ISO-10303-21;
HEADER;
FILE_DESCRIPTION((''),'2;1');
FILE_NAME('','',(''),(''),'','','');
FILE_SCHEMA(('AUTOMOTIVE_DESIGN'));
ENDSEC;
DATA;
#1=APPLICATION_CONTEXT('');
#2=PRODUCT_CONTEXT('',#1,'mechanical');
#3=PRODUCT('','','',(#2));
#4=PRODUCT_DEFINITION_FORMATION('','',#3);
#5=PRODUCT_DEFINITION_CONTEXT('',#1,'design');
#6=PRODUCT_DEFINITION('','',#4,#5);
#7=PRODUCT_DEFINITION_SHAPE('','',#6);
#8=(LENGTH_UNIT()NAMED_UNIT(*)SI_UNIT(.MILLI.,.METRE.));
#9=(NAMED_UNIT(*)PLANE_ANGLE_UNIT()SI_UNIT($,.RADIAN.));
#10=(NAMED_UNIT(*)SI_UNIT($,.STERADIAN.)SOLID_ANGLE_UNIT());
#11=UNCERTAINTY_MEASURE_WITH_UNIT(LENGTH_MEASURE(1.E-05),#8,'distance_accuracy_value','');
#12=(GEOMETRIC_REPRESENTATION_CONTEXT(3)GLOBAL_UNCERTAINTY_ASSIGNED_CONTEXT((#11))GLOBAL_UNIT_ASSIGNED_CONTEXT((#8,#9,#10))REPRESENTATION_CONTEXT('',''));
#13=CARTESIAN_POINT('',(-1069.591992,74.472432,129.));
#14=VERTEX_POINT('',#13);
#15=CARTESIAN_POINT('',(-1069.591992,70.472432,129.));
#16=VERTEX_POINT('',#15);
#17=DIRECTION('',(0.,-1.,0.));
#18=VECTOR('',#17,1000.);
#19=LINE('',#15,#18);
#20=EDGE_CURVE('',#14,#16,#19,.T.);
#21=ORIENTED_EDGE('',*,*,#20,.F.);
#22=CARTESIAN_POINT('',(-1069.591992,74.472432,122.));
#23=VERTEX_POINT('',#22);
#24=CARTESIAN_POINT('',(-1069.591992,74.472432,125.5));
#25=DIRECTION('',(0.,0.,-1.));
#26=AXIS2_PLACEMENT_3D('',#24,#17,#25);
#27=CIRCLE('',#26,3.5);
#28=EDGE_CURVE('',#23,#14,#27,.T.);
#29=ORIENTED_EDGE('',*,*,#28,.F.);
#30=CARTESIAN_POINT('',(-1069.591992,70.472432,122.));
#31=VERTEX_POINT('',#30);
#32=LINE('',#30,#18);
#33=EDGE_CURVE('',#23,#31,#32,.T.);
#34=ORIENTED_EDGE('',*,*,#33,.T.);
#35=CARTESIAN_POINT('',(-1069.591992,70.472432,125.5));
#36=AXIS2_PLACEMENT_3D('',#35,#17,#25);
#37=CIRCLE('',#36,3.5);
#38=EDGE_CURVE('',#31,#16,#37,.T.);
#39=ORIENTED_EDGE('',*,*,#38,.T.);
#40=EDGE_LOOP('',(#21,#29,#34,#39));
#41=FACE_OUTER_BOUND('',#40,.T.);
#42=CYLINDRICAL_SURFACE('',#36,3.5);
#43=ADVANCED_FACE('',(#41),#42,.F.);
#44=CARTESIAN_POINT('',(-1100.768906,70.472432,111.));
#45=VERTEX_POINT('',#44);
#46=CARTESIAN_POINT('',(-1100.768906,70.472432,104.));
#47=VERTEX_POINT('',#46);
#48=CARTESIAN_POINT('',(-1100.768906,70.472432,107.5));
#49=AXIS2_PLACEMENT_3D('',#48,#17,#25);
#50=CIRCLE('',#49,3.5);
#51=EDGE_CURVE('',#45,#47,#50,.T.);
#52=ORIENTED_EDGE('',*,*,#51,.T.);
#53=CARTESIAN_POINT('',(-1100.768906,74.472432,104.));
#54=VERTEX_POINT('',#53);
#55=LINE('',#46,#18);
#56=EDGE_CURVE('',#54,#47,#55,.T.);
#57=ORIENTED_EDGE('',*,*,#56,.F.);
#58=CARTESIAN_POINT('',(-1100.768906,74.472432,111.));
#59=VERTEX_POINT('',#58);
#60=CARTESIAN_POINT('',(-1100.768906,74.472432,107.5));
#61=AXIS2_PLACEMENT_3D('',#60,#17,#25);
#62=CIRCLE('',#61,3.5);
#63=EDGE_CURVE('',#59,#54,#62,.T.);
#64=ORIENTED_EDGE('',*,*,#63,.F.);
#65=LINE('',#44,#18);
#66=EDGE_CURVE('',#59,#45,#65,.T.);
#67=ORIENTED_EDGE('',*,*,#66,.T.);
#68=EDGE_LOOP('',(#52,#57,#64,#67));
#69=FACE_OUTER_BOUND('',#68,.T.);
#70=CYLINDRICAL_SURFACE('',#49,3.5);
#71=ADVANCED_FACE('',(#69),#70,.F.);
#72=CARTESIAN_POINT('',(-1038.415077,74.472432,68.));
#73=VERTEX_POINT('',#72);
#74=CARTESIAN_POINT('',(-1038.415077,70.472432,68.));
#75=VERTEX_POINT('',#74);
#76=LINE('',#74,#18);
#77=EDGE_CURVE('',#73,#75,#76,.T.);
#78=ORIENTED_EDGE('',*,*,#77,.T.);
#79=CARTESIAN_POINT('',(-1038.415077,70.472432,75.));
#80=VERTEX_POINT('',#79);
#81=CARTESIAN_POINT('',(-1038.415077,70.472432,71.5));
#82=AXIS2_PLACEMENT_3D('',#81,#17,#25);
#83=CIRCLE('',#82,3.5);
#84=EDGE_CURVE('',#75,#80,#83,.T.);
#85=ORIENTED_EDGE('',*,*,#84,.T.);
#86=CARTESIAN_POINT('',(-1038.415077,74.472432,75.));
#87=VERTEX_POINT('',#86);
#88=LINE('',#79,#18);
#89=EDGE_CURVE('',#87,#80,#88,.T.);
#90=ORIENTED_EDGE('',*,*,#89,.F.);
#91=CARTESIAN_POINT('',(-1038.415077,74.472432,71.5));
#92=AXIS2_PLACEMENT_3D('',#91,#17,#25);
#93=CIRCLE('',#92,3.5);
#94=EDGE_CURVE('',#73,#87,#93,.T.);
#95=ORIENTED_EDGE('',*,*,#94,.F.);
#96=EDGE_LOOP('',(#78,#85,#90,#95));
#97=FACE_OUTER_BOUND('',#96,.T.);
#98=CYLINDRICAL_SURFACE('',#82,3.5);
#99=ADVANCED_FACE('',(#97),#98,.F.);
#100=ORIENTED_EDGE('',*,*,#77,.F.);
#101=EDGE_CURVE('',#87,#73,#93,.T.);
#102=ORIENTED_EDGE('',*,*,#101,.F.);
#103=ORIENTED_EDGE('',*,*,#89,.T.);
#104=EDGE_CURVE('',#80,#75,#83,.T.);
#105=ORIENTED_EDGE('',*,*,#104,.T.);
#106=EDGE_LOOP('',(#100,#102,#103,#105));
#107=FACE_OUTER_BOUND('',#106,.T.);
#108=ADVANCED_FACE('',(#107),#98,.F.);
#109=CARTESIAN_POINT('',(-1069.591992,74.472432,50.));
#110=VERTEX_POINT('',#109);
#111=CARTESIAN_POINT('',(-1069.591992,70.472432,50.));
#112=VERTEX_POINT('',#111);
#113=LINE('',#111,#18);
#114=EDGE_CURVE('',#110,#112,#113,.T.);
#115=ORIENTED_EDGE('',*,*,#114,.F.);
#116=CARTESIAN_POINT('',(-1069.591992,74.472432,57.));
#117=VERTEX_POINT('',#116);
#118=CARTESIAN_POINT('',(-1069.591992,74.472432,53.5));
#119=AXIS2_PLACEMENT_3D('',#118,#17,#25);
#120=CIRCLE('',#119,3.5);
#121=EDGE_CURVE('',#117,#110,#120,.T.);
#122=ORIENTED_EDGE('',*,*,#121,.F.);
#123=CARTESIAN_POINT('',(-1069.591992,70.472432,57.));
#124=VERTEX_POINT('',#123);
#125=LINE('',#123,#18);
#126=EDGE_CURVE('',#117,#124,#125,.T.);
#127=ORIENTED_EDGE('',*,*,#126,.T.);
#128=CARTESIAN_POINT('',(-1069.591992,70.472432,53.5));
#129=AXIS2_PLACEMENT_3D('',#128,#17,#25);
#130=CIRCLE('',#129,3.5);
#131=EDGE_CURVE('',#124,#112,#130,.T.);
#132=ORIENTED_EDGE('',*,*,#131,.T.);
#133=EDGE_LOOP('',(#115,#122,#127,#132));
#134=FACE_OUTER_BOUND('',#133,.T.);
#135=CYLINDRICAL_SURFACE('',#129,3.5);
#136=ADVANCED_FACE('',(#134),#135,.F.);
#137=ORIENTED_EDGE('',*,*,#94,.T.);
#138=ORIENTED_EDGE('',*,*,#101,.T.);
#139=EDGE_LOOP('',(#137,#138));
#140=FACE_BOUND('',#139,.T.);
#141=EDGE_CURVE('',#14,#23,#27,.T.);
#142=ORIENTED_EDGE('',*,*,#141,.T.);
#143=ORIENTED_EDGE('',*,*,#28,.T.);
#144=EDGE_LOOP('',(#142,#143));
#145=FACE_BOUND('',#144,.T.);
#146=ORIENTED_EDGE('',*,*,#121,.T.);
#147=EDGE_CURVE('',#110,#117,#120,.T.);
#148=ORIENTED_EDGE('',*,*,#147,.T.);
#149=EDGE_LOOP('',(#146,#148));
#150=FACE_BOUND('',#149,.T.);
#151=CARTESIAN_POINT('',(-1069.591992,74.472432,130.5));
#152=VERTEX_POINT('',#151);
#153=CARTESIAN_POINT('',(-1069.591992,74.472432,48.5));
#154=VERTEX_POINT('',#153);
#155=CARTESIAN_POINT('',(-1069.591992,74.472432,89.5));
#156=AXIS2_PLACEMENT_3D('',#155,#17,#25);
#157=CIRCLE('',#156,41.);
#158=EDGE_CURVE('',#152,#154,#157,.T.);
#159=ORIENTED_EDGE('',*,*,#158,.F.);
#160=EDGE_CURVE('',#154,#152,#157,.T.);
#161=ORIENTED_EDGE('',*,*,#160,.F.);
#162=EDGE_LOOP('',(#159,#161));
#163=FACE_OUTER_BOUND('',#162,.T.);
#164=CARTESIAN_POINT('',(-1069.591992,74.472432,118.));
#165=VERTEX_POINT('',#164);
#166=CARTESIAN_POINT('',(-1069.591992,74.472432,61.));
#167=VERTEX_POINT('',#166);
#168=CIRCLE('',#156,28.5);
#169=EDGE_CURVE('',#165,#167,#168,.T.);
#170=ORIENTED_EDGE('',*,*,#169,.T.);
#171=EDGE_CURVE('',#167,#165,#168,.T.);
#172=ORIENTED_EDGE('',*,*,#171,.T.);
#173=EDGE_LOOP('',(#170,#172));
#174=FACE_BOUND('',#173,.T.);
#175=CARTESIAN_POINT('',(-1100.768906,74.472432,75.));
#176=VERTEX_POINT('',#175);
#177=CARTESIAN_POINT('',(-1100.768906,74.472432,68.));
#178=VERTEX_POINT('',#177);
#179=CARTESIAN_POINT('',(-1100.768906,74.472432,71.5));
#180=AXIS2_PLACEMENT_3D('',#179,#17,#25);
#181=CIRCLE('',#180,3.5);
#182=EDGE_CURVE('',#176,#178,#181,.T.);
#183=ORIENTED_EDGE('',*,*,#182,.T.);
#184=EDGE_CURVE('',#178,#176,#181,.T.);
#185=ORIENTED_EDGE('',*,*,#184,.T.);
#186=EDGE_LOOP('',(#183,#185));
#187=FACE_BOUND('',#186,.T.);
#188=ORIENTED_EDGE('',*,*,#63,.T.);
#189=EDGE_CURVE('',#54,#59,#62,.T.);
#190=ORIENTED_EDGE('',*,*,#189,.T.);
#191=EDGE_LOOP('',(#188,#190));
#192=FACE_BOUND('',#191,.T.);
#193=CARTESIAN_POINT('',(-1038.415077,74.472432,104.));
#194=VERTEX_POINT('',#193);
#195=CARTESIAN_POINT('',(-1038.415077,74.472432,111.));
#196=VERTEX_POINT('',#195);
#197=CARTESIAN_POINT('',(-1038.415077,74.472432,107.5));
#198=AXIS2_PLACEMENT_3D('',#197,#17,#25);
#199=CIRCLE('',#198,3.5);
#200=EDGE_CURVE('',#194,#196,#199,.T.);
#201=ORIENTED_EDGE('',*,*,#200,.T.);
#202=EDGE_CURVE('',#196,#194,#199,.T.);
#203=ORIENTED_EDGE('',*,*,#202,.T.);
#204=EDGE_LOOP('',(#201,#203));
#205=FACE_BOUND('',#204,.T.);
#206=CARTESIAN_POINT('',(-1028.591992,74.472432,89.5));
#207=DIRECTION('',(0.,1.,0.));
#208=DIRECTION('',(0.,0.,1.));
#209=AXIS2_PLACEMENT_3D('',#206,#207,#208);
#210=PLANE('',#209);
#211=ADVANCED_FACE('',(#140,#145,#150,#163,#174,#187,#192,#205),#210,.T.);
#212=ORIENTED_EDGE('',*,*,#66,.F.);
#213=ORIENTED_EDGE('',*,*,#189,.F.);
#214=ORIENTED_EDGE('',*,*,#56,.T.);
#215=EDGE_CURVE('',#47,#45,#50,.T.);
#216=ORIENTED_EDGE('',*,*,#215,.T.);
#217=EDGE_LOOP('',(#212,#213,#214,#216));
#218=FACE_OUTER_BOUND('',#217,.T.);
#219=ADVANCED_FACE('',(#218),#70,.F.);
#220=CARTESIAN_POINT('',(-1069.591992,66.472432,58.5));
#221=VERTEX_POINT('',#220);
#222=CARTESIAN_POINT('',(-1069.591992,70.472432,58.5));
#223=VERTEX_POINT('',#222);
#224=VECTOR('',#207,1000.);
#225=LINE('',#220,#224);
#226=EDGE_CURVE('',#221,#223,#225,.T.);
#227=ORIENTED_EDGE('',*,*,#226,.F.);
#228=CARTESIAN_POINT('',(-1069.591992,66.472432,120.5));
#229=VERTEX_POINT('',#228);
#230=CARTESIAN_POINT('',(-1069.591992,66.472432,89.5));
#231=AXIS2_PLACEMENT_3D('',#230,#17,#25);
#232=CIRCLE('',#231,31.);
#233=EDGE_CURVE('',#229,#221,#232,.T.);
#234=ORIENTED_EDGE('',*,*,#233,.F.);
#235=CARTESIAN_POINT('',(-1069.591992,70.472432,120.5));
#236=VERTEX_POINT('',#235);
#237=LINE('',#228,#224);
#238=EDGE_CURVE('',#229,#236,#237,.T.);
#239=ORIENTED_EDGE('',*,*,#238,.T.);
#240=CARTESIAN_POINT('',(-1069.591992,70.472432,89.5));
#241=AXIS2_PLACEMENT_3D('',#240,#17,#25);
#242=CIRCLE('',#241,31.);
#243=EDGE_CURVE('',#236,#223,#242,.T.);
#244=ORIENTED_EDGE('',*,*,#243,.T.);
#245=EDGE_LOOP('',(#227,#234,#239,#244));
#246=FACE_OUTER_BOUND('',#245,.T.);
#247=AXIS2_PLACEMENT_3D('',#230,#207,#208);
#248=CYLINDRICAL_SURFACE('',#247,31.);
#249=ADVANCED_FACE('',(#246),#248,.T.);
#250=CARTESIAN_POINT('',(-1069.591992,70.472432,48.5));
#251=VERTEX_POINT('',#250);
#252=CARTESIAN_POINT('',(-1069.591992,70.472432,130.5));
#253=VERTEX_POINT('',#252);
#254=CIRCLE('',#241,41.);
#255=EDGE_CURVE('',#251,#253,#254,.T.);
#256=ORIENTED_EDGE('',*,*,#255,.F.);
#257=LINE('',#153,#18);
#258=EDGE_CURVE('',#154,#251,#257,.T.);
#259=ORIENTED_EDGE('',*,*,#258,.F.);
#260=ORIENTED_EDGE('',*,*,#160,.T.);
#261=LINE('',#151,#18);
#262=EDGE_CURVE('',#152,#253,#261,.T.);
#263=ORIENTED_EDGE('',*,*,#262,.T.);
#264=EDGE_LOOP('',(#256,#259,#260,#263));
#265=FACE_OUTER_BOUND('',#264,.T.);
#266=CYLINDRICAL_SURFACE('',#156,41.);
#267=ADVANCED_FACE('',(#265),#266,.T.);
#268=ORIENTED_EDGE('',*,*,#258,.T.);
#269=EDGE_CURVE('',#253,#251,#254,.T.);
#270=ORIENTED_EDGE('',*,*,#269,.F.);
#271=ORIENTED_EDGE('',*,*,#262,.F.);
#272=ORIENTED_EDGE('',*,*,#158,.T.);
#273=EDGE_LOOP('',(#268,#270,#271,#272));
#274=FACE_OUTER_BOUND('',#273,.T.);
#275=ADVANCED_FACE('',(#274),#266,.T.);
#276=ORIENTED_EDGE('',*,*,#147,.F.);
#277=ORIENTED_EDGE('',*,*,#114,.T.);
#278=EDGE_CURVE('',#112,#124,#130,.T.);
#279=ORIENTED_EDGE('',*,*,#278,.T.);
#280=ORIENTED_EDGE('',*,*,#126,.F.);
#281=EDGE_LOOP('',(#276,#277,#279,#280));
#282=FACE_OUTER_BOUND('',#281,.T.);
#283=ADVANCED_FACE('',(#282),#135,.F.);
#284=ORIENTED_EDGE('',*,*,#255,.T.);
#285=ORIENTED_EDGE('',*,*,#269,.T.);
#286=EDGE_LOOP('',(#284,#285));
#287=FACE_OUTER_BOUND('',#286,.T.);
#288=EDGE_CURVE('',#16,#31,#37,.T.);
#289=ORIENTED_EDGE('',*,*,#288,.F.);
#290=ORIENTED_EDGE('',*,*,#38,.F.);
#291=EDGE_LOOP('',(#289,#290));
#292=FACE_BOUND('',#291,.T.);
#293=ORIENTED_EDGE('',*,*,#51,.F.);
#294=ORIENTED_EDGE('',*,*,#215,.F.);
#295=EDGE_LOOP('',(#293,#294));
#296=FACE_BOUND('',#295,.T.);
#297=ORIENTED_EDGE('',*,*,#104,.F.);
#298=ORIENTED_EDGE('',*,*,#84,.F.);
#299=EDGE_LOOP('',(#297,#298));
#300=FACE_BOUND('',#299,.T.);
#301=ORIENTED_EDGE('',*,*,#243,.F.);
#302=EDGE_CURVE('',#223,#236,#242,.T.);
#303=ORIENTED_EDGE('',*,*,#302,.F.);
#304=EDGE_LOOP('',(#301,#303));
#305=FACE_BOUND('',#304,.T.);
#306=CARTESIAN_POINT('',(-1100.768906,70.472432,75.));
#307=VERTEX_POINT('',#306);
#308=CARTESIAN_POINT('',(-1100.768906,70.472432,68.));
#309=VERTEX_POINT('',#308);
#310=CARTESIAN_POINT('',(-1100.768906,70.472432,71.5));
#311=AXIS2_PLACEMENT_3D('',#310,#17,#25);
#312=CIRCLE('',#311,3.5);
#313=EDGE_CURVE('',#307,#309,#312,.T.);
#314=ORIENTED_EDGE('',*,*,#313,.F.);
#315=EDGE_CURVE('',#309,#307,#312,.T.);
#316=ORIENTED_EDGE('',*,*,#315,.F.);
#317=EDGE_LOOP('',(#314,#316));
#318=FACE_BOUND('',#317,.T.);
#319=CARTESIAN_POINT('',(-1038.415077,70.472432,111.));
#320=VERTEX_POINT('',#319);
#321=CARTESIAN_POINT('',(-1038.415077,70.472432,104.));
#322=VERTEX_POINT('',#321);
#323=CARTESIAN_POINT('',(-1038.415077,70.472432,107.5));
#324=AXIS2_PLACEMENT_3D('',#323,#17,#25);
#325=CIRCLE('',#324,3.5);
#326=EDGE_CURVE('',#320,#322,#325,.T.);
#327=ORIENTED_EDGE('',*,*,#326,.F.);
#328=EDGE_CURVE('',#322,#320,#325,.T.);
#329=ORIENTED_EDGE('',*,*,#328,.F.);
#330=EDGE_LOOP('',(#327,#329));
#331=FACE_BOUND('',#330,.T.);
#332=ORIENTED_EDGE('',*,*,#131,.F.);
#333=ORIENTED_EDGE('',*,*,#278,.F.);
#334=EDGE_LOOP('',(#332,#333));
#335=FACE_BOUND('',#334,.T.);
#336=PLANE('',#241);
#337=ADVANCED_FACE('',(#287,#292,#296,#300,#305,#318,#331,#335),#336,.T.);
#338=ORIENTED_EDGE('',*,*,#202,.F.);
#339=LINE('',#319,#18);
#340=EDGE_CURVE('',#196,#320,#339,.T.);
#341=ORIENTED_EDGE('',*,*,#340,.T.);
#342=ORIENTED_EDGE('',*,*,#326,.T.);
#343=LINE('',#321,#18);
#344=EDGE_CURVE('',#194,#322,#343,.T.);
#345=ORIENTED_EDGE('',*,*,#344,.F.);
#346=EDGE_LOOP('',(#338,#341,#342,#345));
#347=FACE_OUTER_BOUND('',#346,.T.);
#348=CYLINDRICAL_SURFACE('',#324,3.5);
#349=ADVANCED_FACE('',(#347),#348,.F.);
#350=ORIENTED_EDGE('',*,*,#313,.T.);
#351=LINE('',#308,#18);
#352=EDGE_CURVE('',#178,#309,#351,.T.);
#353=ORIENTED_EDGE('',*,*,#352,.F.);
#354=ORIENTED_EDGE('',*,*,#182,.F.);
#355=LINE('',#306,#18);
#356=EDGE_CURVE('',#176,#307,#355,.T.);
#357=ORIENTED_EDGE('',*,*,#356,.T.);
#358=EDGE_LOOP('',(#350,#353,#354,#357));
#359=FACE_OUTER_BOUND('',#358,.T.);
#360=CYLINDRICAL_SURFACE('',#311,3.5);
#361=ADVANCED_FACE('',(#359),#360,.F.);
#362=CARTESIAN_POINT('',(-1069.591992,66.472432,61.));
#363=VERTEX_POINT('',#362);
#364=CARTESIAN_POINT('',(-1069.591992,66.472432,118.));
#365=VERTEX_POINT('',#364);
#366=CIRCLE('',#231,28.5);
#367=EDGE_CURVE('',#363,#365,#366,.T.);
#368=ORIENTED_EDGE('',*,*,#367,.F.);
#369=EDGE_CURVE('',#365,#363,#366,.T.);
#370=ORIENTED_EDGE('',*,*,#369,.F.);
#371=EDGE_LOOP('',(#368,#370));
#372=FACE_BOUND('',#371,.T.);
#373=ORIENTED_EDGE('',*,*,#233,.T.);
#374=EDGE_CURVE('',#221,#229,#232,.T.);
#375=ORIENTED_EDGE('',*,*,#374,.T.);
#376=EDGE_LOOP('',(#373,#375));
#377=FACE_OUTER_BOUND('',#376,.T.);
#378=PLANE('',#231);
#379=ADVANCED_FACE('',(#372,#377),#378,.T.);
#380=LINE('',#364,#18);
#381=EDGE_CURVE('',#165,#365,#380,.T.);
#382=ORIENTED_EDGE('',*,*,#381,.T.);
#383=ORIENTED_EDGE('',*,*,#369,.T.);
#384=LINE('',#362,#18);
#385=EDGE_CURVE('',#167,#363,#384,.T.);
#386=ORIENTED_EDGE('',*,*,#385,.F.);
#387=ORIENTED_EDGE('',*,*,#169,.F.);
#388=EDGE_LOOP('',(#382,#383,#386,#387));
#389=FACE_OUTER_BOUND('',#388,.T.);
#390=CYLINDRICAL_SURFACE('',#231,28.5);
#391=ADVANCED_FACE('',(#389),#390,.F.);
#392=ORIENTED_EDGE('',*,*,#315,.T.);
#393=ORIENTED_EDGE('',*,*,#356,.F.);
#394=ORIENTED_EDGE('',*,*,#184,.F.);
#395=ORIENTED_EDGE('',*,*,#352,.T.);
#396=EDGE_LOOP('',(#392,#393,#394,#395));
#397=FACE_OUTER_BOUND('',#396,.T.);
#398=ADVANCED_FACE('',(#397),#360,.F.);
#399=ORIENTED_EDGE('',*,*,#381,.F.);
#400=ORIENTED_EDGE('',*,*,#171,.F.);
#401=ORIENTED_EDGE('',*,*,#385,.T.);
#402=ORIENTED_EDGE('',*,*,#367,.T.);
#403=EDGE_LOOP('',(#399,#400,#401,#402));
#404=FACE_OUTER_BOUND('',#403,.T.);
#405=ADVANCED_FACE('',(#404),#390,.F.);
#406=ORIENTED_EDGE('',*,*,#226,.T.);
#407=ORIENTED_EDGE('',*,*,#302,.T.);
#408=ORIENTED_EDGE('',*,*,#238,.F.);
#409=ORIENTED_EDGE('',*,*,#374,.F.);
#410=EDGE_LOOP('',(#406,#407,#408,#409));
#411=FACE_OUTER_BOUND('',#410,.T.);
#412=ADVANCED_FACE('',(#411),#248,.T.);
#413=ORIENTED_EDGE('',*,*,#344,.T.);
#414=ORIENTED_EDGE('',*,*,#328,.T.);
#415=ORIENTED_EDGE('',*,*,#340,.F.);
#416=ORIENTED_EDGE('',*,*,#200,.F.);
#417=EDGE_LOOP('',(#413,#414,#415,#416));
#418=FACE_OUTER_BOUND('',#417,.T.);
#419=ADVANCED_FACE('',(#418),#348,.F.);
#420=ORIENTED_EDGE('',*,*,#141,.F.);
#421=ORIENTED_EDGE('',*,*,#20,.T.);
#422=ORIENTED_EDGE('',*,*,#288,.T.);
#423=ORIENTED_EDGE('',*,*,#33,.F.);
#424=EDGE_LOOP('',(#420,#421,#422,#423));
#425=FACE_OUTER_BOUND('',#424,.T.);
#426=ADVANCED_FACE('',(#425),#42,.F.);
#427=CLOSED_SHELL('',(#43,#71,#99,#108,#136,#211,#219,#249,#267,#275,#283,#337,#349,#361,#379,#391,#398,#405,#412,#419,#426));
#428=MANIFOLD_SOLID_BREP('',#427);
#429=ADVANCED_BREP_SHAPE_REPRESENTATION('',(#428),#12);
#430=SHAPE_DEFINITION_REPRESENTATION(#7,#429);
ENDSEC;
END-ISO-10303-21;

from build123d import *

# Parameters (mm, degrees)
SKETCH1_W                = 41
SKETCH1_H                = 4
SKETCH2_R                = 31
BOSS_EXTRUDE1_DEPTH      = 4
M52_CLEARANCE_HOLE1_D    = 57
F_7_0_7_DIAMETER_HOLE1_D = 7


with BuildPart() as part:
    # Sketch1 → Revolve1 (revolve)
    with BuildSketch(Plane.XY.offset(89.5), mode=Mode.PRIVATE) as revolve1_sk:
        with Locations((-1049.091991574, 72.472431577)):
            Rectangle(SKETCH1_W, SKETCH1_H)
    revolve(revolve1_sk.sketch.rotate(Axis((-1069.591991574, 74.472431577, 89.5), (0, -1, 0)), 270), axis=Axis((-1069.591991574, 74.472431577, 89.5), (0, -1, 0)))

    # Sketch2 → Boss-Extrude1 (add)
    with BuildSketch(Plane.XZ.offset(-70.472431577)):
        with Locations(Location((-1069.591991574, 89.5, 0), (0, 0, 270))):
            Circle(SKETCH2_R)
    extrude(amount=BOSS_EXTRUDE1_DEPTH)

    # M52 Clearance Hole1 (through all)
    with Locations(Plane(origin=(0, 66.472431577, 0), x_dir=(-1, 0, 0), z_dir=(0, -1, 0))):
        with Locations((1069.591991574, -89.5)):
            Hole(M52_CLEARANCE_HOLE1_D / 2)

    # Ø7.0 (7) Diameter Hole1 (through all)
    with Locations(Plane(origin=(0, 70.472431577, 0), x_dir=(-1, 0, 0), z_dir=(0, -1, 0))):
        with Locations((1069.591991574, -125.5), (1100.76890611, -107.5), (1100.76890611, -71.5), (1069.591991574, -53.5), (1038.415077038, -71.5), (1038.415077038, -107.5)):
            Hole(F_7_0_7_DIAMETER_HOLE1_D / 2)


solid = part.part
